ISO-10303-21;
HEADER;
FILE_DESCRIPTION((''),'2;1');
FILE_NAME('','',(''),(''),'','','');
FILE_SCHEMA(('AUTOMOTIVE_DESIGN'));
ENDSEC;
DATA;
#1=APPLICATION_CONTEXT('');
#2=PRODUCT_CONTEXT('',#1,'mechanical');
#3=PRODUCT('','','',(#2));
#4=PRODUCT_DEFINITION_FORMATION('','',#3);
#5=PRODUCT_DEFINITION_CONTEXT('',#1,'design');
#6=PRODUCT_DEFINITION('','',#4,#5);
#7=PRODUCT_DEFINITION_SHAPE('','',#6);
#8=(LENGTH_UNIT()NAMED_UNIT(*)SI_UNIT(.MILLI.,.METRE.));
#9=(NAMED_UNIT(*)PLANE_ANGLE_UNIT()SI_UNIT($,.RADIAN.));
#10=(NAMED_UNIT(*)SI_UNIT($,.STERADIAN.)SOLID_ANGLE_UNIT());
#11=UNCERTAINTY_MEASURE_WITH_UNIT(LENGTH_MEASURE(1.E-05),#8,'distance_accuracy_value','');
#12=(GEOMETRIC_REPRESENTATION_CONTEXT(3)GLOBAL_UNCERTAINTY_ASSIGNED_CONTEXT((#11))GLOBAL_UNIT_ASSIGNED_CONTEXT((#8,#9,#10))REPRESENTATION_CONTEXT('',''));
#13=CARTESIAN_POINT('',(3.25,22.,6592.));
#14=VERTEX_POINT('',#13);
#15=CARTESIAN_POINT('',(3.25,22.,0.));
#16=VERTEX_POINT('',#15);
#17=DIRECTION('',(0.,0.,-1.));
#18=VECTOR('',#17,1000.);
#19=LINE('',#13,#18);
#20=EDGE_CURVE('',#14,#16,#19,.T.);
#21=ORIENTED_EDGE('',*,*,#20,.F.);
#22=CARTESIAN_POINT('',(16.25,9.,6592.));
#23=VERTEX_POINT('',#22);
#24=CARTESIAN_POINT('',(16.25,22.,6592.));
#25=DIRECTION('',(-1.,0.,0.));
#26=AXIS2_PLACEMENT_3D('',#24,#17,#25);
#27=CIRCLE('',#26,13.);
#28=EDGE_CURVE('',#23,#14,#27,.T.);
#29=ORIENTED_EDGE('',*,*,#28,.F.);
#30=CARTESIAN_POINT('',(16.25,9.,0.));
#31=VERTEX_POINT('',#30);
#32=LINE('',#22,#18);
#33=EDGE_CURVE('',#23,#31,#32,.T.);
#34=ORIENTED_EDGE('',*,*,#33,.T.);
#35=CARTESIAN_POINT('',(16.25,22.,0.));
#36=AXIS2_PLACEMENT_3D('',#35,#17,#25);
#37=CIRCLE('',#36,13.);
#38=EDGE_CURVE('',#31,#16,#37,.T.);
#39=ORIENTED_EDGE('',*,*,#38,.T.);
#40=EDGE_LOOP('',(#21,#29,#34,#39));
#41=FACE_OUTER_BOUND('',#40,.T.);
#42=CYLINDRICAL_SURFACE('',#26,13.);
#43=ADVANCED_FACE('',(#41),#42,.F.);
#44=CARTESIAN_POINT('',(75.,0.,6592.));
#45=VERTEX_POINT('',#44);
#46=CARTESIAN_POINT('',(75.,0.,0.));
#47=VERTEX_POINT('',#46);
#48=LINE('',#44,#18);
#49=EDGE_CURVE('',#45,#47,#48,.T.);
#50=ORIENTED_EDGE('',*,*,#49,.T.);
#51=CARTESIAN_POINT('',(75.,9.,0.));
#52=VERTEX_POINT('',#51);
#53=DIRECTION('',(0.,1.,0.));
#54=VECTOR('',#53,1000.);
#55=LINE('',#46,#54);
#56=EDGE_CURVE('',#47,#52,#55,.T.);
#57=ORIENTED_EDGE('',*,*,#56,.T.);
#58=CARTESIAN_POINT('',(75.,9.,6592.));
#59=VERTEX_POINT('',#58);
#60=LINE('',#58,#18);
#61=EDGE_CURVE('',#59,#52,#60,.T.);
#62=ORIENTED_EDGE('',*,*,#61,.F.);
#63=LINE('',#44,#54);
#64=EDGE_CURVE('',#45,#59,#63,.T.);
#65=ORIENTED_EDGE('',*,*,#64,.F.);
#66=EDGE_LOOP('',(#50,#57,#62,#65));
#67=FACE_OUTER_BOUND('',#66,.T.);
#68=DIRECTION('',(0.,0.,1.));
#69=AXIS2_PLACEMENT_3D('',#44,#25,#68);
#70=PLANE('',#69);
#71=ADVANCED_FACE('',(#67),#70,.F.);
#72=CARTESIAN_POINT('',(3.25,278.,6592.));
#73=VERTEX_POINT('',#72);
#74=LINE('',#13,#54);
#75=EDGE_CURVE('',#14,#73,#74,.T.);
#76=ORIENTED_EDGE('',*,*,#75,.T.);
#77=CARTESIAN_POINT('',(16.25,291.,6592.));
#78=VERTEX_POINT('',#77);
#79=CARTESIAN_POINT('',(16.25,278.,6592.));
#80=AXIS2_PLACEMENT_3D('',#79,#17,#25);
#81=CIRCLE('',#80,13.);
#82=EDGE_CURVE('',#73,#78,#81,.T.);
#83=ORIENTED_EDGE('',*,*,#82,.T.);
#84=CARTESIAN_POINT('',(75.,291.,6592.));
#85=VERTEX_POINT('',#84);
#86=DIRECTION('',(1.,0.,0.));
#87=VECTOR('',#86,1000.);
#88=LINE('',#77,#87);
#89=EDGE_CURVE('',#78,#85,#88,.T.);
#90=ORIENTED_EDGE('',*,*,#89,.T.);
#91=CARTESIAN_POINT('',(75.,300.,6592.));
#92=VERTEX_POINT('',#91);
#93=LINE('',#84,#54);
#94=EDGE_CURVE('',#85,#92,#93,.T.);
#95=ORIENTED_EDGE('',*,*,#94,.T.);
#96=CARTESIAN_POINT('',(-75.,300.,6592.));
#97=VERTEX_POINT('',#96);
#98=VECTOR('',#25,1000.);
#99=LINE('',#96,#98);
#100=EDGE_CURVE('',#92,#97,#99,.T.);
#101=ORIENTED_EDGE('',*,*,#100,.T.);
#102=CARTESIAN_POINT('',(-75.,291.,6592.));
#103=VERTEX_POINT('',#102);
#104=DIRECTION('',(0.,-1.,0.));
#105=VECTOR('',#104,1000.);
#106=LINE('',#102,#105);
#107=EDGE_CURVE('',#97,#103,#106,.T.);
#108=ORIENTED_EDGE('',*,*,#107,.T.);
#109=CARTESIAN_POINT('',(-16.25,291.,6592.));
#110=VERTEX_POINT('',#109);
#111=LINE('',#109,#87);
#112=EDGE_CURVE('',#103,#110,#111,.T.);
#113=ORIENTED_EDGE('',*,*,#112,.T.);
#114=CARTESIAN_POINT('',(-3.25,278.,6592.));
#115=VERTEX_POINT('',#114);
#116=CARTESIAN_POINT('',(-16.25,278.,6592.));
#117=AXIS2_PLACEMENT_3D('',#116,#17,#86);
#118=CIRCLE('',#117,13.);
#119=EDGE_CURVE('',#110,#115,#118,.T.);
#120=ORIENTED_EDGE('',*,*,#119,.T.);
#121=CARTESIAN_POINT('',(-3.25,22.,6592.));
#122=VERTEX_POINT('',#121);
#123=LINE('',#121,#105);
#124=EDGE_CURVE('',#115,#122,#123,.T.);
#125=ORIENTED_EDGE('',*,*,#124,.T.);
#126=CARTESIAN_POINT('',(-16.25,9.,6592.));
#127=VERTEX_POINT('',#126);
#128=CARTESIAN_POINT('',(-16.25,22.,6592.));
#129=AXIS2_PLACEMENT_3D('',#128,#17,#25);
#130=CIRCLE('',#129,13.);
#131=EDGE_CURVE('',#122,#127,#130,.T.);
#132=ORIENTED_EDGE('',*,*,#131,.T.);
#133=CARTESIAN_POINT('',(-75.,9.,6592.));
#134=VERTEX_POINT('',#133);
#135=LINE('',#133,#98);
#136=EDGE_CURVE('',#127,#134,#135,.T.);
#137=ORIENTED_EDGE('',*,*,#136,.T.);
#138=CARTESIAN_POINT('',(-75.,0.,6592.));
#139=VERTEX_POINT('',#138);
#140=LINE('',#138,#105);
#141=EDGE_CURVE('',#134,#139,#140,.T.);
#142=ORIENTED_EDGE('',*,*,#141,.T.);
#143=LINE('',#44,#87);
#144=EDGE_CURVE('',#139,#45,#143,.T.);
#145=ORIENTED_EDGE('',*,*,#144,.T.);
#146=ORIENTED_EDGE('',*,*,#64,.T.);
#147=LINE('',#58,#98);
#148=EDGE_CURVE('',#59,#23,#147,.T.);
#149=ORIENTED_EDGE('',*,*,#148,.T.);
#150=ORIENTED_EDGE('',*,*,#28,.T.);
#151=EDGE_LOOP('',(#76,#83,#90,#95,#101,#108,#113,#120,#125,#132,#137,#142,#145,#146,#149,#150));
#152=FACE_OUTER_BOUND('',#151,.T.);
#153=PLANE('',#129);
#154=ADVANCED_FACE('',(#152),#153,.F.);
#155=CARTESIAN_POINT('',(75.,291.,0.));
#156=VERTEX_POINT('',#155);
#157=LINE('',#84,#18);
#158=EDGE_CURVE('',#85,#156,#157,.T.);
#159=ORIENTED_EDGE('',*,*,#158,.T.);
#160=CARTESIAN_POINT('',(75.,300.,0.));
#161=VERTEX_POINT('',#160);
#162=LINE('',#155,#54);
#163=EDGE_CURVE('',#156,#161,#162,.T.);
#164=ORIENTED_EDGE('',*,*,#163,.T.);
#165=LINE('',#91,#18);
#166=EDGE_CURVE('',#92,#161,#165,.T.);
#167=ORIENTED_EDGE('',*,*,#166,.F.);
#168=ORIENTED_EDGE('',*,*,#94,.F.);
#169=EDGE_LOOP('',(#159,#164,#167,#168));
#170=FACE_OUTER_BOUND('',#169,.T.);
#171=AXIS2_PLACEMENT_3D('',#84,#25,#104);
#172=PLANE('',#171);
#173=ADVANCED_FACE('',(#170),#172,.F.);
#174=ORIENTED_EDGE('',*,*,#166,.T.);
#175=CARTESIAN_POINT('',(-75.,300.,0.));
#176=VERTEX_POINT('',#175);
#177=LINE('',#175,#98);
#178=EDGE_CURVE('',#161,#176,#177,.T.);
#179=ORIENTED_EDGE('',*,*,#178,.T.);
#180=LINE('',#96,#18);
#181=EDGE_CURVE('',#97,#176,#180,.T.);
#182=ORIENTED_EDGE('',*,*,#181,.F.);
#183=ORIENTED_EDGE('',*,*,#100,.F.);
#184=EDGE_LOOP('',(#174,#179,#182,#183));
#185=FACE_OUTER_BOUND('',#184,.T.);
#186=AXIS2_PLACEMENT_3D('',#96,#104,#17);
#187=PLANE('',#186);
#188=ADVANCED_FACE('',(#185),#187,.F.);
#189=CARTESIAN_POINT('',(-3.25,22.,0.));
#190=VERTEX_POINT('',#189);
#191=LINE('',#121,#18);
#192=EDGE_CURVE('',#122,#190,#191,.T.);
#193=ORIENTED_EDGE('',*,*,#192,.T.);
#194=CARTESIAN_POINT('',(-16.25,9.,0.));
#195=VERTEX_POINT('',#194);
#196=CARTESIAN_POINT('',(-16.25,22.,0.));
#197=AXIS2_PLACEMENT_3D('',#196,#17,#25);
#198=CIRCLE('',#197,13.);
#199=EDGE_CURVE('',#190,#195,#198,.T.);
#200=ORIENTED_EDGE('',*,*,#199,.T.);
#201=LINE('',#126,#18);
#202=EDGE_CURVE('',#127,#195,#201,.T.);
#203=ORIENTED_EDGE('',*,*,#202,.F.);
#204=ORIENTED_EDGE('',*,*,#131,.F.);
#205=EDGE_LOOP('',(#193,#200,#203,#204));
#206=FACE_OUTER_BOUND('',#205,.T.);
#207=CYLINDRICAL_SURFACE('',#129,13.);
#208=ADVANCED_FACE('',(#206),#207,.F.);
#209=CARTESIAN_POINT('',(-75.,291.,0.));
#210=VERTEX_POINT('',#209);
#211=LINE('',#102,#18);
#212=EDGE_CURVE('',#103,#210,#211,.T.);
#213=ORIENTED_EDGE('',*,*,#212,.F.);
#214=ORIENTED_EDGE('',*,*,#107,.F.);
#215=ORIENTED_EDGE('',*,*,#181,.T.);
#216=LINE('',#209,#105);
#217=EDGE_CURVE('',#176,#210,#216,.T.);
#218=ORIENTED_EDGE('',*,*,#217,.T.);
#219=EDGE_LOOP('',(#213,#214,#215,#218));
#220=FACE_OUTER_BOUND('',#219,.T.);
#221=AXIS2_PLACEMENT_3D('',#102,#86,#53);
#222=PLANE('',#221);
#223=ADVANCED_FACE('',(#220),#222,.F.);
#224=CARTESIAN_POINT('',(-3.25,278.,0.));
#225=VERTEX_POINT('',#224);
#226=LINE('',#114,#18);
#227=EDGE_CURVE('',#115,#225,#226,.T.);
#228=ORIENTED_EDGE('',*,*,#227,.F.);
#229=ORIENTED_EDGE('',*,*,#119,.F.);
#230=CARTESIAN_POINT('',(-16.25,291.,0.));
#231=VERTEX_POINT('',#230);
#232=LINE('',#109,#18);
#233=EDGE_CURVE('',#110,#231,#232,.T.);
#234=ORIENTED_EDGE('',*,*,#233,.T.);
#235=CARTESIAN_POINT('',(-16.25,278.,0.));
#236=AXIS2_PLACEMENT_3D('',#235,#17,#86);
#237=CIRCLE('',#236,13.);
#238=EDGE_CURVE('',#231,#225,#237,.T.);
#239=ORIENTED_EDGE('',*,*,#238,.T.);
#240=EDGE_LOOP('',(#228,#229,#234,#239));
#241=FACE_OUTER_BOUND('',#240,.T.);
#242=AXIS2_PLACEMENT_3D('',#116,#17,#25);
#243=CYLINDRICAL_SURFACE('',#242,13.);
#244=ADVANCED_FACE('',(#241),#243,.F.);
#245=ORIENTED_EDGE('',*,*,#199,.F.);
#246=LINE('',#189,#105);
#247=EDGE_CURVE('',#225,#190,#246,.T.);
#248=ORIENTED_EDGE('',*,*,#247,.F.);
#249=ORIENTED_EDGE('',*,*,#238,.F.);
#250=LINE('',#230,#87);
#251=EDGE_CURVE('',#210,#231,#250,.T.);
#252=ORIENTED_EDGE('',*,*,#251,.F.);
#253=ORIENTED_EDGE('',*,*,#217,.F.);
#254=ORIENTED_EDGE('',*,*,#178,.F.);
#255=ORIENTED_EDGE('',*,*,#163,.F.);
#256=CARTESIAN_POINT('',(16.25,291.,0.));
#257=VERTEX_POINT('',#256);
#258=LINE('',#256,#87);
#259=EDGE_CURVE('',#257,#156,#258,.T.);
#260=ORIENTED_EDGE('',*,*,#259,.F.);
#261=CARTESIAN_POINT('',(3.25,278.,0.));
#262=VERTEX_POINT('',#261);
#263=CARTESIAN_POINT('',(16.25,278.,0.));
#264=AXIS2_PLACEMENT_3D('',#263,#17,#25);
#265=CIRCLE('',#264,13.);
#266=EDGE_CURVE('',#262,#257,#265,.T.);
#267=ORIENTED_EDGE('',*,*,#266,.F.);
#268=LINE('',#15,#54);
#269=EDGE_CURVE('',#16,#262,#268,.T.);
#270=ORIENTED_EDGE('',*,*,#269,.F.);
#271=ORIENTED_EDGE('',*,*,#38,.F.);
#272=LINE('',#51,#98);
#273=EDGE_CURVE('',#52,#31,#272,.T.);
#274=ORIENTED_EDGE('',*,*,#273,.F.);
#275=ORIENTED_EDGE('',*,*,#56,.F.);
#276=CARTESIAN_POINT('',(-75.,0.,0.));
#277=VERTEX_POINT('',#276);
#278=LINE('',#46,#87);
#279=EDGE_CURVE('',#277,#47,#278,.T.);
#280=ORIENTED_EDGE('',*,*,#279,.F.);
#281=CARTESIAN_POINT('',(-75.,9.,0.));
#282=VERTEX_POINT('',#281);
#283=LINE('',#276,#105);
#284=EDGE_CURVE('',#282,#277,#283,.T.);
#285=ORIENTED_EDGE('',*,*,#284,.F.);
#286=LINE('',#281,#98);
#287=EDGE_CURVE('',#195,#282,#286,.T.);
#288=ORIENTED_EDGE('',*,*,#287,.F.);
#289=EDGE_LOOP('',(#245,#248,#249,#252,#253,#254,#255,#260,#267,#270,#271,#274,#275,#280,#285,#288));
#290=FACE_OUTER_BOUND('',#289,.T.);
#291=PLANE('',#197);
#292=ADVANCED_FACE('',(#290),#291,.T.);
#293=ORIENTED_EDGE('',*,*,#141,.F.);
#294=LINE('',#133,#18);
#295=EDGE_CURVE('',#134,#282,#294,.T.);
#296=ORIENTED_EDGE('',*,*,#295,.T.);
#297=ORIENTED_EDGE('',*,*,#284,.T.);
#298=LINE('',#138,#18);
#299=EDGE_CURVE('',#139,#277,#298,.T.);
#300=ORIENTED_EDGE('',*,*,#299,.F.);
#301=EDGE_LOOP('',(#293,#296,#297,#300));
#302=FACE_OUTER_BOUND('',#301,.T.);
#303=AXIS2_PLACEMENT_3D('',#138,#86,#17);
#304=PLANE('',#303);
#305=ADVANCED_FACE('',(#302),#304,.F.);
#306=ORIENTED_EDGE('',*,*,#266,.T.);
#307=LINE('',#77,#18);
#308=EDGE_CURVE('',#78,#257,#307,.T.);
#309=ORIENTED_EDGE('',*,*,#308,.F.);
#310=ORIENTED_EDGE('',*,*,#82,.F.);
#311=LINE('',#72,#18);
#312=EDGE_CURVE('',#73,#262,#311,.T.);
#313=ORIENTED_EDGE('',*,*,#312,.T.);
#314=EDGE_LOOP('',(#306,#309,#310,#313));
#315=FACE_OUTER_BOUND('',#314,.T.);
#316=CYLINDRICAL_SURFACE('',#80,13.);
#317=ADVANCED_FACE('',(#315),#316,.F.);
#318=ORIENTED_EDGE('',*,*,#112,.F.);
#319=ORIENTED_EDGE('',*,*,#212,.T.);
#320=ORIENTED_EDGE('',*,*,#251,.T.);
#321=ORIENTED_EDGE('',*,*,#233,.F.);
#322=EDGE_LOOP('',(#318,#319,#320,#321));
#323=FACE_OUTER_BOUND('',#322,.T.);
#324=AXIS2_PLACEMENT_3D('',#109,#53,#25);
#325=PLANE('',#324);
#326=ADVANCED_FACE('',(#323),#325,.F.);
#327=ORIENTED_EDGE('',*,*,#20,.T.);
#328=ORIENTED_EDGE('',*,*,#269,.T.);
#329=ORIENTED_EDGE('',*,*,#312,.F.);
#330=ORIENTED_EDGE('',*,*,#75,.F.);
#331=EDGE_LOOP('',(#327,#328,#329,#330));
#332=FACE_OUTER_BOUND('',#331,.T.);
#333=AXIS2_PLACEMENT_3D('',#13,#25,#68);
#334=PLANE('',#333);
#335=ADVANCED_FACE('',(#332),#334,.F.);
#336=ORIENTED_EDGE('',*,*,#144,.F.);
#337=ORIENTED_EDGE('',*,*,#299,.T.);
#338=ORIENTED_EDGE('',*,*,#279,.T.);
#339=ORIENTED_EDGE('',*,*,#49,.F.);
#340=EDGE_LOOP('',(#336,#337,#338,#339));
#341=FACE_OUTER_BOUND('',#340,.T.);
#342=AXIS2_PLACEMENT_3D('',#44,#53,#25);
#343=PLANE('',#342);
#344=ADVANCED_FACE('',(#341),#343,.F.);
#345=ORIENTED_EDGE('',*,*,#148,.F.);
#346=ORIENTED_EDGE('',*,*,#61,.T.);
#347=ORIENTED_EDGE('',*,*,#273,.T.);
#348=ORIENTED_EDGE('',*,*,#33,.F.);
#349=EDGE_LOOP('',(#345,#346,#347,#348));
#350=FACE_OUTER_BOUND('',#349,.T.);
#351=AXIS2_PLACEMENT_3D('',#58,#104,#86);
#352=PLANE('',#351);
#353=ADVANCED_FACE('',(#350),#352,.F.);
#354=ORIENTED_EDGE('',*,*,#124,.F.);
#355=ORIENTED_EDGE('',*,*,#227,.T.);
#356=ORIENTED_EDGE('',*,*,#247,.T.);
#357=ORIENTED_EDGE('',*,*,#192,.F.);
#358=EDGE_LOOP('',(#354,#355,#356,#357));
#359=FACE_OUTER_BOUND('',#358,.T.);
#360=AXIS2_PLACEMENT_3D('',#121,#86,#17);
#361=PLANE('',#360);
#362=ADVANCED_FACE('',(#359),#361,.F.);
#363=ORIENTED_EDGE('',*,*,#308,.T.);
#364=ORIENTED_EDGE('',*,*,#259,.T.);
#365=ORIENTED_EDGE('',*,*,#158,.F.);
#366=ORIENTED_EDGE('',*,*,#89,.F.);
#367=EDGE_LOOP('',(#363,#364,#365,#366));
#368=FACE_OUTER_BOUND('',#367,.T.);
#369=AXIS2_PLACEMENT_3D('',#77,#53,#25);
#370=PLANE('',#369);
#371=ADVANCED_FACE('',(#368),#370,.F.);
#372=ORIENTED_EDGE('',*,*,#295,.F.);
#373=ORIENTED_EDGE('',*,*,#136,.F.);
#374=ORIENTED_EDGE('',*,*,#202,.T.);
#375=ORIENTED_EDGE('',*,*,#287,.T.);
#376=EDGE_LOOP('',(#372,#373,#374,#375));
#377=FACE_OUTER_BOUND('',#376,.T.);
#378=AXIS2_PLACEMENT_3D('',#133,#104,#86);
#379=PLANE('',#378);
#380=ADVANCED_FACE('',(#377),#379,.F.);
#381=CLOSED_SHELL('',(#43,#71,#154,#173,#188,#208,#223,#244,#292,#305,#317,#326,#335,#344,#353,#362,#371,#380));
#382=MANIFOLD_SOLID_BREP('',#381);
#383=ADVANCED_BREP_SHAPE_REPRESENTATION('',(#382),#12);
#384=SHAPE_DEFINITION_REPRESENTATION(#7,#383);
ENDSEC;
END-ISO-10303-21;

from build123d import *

# Parameters (mm, degrees)
BOSS_EXTRUDE1_DEPTH = 6592


with BuildPart() as part:
    # Sketch1 → Boss-Extrude1 (new body)
    with BuildSketch(Plane.XY):
        with BuildLine():
            Line((75, 0), (-75, 0))
            Line((-75, 0), (-75, 9))
            Line((-75, 9), (-16.25, 9))
            ThreePointArc((-16.25, 9), (-7.057611845, 12.807611845), (-3.25, 22))
            Line((-3.25, 22), (-3.25, 278))
            ThreePointArc((-3.25, 278), (-7.057611845, 287.192388155), (-16.25, 291))
            Line((-16.25, 291), (-75, 291))
            Line((-75, 291), (-75, 300))
            Line((-75, 300), (75, 300))
            Line((75, 300), (75, 291))
            Line((75, 291), (16.25, 291))
            ThreePointArc((16.25, 291), (7.057611845, 287.192388155), (3.25, 278))
            Line((3.25, 278), (3.25, 22))
            ThreePointArc((3.25, 22), (7.057611845, 12.807611845), (16.25, 9))
            Line((16.25, 9), (75, 9))
            Line((75, 9), (75, 0))
        make_face()
    extrude(amount=BOSS_EXTRUDE1_DEPTH)


solid = part.part
